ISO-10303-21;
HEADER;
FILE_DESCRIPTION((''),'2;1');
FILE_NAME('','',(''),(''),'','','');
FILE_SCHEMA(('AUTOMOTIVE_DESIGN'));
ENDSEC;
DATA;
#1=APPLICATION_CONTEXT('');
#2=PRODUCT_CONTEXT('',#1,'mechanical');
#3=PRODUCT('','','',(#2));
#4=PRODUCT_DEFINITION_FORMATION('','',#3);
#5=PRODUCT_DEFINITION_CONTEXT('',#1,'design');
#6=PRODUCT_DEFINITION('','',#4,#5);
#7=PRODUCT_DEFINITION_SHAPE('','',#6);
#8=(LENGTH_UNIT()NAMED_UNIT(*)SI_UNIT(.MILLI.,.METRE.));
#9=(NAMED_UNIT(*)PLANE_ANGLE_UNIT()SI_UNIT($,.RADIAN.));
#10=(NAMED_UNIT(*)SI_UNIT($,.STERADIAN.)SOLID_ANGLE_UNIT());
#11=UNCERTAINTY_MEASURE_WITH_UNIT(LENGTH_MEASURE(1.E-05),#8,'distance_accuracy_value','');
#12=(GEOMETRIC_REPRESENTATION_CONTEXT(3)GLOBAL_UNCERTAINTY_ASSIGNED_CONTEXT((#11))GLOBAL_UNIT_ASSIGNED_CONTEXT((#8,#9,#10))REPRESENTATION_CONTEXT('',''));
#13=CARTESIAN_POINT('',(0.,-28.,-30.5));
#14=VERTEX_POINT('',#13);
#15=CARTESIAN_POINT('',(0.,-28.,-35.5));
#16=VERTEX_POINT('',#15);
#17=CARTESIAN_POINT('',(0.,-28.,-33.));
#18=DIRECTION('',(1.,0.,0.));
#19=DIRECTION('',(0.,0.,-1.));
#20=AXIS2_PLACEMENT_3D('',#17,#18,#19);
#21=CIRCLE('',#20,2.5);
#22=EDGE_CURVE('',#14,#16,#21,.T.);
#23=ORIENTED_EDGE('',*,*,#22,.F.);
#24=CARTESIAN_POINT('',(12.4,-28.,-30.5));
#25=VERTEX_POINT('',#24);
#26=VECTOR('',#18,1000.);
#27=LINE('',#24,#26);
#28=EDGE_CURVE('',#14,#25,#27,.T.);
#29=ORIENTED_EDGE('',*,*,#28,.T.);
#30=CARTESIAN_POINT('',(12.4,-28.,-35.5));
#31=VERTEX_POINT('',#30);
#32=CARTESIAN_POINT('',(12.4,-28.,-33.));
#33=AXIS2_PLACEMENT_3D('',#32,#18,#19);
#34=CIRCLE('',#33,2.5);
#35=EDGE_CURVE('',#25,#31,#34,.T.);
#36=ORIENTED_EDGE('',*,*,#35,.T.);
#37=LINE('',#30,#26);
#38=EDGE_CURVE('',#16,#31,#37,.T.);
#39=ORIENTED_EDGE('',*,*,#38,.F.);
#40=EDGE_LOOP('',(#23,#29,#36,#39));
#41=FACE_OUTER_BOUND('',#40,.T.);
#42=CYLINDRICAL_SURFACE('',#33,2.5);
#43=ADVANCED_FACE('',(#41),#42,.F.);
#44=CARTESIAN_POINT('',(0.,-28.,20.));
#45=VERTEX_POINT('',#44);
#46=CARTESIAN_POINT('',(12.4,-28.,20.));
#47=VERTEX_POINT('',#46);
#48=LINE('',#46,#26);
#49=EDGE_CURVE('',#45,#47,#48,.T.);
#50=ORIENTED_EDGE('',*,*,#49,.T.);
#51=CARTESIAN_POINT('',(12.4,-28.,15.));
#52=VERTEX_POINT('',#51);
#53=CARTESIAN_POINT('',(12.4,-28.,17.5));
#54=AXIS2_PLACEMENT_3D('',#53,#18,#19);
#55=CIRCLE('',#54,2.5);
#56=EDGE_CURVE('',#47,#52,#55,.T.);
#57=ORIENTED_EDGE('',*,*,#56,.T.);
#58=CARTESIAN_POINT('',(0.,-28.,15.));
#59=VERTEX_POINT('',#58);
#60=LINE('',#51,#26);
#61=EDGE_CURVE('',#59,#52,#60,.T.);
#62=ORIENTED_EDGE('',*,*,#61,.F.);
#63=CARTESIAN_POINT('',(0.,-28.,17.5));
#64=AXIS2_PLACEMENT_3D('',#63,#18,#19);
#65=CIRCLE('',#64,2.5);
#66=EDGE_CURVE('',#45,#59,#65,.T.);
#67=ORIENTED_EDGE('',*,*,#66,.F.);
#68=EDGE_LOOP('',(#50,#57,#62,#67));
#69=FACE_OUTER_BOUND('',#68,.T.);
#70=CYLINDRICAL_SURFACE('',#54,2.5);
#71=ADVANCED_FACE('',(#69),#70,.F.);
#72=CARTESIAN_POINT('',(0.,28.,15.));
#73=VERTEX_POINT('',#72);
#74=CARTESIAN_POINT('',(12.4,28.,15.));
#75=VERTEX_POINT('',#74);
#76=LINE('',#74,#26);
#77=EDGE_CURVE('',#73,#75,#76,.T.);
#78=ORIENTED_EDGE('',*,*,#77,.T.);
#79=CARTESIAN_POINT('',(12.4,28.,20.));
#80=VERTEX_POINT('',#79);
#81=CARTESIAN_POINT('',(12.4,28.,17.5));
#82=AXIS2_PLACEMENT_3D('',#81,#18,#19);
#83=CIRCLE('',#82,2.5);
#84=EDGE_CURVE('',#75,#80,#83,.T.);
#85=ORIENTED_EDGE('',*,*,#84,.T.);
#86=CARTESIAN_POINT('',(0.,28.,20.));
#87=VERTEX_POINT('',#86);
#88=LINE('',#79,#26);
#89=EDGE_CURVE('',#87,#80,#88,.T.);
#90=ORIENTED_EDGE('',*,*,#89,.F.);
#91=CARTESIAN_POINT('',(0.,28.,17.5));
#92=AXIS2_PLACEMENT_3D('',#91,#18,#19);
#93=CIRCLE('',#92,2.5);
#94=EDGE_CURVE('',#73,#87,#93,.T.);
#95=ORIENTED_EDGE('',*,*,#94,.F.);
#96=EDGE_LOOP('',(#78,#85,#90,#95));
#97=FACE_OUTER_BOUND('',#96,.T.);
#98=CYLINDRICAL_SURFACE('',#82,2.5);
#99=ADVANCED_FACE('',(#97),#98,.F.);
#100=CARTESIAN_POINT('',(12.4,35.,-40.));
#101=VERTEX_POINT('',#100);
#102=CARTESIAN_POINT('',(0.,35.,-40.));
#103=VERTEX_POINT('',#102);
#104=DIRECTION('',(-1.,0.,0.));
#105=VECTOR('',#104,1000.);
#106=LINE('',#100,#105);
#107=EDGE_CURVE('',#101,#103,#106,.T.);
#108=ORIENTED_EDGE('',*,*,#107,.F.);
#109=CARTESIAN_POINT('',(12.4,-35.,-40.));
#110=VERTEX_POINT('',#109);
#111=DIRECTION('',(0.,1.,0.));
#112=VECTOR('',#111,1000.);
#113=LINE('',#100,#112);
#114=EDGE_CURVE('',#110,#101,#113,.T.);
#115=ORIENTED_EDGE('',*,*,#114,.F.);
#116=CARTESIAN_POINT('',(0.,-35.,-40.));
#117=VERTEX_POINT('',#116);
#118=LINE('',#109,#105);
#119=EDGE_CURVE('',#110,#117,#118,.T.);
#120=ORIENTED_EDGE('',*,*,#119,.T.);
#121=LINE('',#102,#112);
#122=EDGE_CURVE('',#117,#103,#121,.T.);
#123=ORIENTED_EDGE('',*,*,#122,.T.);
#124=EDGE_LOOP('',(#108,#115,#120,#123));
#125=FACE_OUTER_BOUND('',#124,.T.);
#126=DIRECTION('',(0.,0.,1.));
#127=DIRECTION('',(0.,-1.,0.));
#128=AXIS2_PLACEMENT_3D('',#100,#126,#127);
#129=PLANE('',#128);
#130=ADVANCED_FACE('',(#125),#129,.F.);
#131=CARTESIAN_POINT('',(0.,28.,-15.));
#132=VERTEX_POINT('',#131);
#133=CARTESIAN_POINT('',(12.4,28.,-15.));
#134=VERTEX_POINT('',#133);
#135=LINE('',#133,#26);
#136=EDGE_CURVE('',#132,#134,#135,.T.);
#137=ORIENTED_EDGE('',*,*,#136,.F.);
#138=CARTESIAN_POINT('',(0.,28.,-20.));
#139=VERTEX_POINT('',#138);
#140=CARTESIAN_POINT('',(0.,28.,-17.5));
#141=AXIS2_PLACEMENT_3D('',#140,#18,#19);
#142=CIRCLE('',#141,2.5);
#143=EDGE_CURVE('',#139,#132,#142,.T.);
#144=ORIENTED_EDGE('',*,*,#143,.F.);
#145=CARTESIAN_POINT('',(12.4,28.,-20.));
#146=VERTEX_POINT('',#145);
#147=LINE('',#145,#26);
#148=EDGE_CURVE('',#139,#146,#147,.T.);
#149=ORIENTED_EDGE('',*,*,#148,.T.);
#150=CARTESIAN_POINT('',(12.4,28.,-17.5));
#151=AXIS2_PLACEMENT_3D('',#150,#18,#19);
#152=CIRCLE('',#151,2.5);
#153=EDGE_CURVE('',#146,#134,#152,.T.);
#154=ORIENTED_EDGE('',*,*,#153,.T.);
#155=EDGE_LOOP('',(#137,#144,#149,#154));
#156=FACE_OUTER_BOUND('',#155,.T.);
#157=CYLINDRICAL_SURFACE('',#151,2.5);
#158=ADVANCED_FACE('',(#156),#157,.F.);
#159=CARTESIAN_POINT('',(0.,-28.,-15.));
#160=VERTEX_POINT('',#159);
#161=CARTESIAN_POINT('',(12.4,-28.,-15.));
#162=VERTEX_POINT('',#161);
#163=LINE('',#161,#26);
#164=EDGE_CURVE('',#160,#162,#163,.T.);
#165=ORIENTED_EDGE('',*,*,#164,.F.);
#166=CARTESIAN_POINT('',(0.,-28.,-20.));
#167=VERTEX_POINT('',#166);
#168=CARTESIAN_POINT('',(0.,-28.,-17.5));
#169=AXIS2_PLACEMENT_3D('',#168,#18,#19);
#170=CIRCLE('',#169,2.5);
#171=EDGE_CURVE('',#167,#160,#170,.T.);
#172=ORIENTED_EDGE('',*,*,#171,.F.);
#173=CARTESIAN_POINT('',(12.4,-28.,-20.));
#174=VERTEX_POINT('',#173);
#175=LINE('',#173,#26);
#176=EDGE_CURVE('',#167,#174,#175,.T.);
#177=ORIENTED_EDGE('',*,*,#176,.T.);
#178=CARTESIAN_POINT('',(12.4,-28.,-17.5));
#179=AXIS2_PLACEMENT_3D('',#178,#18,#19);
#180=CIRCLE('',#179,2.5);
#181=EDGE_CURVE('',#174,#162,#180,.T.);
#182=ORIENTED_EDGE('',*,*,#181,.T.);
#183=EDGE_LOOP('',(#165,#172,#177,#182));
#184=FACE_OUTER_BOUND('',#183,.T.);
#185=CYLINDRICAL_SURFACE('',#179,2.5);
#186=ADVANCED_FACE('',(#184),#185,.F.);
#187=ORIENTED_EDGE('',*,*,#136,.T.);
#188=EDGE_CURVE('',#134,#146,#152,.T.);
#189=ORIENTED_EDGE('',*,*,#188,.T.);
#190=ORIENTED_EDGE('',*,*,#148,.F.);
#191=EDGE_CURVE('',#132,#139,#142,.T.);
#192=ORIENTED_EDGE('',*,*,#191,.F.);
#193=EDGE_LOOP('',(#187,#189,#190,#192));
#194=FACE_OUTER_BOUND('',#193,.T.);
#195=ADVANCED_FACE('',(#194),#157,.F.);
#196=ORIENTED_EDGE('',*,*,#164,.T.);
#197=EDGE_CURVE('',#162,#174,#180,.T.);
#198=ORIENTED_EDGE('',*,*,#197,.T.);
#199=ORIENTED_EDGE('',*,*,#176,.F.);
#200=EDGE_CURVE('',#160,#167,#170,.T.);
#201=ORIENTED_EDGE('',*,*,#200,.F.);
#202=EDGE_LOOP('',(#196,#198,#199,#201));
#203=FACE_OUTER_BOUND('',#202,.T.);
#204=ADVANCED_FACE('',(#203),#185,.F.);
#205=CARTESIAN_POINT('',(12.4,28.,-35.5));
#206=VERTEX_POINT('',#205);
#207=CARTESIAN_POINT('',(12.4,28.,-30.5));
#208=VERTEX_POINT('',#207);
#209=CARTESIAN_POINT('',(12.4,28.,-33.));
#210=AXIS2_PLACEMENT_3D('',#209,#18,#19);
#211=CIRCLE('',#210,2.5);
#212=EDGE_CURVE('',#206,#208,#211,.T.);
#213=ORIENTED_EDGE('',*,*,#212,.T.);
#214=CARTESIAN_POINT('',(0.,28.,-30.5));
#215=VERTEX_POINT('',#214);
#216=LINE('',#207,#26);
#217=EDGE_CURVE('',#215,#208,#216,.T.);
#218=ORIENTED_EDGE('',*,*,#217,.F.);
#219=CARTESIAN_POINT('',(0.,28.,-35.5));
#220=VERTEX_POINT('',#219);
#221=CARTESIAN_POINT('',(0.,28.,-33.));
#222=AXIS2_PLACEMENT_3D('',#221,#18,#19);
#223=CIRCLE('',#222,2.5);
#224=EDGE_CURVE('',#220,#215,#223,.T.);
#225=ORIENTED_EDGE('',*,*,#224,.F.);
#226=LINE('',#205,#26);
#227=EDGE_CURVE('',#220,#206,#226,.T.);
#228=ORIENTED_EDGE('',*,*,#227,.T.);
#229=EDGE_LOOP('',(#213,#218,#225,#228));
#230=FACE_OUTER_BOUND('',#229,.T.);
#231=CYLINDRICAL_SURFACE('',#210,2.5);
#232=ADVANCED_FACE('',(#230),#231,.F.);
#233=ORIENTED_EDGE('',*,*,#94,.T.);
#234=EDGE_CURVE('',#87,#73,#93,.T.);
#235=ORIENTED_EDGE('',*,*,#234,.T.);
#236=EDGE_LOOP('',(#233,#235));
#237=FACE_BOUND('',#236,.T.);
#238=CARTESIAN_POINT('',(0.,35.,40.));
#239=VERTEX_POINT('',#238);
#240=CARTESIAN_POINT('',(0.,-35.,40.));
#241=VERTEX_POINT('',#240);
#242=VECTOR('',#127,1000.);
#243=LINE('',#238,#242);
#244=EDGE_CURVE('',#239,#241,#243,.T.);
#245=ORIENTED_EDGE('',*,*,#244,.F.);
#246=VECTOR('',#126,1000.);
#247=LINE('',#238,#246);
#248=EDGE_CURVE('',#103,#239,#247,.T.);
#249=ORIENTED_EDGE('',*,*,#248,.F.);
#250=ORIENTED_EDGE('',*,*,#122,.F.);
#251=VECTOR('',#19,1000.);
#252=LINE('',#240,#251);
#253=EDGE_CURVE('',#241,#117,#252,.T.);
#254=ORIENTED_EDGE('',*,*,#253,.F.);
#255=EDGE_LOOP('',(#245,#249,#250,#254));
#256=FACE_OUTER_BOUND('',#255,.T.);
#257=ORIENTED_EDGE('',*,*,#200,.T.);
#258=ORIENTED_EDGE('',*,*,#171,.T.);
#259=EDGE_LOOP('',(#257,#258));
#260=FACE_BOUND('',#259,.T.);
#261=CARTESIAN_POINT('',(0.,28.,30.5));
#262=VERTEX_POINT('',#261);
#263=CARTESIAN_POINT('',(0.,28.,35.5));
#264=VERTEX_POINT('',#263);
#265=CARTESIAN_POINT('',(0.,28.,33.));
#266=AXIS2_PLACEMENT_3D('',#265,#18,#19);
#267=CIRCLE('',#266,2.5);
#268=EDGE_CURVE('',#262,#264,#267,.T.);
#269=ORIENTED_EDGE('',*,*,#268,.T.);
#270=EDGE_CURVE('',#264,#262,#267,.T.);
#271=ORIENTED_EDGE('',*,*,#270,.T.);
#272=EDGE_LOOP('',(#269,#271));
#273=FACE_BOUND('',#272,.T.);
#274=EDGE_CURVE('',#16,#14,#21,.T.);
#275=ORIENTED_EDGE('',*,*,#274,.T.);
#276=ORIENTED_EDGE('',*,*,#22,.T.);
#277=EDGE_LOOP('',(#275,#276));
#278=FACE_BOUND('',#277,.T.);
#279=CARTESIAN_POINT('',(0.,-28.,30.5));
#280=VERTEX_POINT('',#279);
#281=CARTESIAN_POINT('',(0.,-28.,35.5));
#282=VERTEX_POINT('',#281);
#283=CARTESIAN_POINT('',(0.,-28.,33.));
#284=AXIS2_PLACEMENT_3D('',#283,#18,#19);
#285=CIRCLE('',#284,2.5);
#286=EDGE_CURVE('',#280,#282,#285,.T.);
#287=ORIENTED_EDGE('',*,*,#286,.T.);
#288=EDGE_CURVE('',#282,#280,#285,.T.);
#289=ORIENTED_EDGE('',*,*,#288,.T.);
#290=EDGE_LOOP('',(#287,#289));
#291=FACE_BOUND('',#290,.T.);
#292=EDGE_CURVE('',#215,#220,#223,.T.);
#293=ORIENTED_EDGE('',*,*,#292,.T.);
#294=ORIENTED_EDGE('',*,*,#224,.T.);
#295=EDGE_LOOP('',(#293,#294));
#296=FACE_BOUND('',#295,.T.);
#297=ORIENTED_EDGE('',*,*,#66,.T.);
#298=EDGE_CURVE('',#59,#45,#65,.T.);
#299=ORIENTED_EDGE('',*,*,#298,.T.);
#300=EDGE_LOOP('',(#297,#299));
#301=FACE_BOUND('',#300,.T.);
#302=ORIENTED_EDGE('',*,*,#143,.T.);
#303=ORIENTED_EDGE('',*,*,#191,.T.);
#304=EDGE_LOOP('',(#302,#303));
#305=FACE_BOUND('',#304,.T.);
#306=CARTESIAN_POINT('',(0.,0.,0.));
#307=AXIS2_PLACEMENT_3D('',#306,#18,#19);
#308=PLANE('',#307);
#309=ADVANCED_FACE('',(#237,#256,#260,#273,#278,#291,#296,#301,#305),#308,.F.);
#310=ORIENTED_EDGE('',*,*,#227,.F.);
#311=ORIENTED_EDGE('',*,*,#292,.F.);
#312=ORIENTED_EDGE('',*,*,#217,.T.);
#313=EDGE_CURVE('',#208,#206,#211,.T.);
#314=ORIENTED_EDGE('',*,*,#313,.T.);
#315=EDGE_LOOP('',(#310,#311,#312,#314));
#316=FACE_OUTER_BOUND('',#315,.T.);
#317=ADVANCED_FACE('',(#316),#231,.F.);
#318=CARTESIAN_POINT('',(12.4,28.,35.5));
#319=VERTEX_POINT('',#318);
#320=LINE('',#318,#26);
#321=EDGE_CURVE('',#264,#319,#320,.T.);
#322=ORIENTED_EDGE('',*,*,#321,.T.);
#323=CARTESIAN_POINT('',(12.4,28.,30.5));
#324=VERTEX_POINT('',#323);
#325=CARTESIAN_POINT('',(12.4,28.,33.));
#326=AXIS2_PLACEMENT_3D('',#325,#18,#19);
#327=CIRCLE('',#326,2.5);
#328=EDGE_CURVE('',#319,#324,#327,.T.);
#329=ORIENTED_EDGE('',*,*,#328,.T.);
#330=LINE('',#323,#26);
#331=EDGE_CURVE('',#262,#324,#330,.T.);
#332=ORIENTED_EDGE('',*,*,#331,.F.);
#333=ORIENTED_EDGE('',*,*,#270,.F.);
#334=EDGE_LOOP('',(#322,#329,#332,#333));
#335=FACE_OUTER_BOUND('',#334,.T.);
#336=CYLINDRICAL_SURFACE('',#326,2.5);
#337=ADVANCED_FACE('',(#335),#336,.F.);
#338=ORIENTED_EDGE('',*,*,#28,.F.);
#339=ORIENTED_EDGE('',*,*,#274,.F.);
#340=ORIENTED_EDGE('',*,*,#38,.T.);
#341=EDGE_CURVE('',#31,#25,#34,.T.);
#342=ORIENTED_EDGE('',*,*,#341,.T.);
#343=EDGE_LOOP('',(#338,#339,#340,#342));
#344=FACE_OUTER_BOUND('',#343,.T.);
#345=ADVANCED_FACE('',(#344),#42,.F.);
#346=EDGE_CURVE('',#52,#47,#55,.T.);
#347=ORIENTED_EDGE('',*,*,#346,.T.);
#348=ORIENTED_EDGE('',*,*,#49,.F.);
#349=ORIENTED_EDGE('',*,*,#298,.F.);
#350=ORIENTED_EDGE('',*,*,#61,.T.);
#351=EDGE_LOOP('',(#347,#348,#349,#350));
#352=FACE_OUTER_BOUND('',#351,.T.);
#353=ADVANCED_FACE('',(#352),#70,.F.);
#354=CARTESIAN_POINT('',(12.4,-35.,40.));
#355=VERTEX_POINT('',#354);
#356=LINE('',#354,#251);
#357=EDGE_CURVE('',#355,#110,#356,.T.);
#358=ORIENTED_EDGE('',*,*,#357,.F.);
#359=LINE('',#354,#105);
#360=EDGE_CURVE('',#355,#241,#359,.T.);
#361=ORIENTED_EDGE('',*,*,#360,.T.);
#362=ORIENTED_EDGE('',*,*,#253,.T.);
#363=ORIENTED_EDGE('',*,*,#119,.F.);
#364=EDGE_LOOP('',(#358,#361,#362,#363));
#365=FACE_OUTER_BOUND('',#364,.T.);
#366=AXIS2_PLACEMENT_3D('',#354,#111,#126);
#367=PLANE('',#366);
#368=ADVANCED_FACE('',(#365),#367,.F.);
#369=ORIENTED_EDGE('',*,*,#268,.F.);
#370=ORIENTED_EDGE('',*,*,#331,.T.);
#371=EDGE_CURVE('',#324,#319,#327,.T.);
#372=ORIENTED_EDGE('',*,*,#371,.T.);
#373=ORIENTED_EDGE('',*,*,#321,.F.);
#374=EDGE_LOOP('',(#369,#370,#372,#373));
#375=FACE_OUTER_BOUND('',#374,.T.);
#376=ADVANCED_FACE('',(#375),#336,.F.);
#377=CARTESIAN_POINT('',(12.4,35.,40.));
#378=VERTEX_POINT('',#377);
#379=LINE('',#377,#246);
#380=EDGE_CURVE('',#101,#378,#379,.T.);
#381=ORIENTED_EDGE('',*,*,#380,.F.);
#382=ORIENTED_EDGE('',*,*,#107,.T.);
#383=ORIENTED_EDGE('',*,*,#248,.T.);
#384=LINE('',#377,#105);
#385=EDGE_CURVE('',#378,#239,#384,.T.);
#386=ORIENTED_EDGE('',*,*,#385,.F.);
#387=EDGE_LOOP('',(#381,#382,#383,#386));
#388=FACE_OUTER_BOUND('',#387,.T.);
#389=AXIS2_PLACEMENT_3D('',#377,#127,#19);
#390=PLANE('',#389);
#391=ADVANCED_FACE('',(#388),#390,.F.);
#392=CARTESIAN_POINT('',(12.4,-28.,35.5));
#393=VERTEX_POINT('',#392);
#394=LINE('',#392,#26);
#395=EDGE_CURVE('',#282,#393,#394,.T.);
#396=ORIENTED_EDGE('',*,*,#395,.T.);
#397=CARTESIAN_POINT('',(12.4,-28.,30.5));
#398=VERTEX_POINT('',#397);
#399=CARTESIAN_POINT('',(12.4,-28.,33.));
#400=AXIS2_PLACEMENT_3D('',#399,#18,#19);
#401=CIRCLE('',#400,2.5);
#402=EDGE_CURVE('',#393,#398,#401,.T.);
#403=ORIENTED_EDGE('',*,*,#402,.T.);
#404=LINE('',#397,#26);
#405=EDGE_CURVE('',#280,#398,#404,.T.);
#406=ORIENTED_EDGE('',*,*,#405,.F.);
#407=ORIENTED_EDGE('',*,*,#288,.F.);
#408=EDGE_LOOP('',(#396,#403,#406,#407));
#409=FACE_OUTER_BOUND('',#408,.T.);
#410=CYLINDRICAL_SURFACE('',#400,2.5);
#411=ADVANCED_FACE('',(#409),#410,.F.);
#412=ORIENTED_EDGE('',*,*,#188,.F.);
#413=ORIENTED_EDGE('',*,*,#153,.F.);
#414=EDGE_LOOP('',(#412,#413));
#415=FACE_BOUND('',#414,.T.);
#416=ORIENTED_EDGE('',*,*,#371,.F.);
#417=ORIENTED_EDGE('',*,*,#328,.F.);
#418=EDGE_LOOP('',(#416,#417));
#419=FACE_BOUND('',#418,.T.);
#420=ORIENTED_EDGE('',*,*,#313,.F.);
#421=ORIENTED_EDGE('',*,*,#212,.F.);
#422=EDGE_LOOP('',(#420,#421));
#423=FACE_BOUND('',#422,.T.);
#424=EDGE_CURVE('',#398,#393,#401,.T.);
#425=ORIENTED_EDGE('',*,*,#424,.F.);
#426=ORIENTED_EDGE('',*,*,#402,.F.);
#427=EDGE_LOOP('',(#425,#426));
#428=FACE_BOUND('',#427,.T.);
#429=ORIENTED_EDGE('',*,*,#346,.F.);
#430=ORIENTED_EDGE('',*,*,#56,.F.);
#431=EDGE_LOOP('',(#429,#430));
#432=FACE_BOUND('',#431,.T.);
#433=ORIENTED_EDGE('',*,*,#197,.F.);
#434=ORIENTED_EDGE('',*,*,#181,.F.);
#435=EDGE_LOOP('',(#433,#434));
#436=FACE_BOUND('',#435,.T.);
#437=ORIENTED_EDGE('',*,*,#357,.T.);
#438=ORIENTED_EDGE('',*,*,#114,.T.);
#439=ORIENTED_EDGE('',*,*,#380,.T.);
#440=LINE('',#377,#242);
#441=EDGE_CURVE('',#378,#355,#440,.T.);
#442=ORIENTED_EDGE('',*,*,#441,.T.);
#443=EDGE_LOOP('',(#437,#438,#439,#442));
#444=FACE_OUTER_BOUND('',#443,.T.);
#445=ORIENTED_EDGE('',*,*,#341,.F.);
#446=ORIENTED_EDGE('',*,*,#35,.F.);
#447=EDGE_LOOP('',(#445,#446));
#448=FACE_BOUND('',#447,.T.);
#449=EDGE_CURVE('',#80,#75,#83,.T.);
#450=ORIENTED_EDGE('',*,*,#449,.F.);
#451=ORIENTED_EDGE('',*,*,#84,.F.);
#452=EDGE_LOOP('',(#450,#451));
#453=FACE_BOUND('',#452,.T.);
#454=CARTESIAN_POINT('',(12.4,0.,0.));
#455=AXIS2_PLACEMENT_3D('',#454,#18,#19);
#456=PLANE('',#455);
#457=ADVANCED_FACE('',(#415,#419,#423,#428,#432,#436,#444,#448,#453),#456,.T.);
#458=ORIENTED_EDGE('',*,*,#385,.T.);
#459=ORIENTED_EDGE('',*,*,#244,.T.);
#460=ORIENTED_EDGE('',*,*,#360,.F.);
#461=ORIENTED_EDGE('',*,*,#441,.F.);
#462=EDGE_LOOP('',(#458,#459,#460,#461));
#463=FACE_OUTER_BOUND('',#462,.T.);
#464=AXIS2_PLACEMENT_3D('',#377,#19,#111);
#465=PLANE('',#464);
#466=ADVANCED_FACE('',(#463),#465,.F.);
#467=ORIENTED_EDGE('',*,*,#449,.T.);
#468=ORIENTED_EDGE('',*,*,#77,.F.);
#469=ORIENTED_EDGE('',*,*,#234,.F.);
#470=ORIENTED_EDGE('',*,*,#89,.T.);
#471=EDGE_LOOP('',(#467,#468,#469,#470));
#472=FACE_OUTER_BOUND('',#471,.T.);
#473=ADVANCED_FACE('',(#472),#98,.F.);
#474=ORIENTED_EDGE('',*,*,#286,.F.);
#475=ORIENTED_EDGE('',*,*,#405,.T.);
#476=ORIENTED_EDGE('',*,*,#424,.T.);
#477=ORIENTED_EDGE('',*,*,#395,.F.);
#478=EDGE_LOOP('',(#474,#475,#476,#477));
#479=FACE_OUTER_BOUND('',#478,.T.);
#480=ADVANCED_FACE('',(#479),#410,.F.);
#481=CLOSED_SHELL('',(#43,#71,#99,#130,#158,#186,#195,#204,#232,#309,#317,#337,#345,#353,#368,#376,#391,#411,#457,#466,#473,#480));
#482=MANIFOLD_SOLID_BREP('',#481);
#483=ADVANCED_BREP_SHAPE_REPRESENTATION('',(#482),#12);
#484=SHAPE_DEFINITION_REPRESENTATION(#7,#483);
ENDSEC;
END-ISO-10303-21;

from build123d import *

# Parameters (mm, degrees)
SKETCH_1_W             = 80
SKETCH_1_H             = 70
EXTRUDE_1_DEPTH        = 12.4
HOLE_WIZARD_M6_1_D     = 5
HOLE_WIZARD_M6_1_DEPTH = 15
HOLE_WIZARD_M6_1_TIP   = 1.502151548
HOLE_WIZARD_M6_2_D     = 5


with BuildPart() as part:
    # 草图1 → 凸台-拉伸1 (new body)
    with BuildSketch(Plane(origin=(0, 0, 0), x_dir=(0, 0, -1), z_dir=(1, 0, 0))):
        Rectangle(SKETCH_1_W, SKETCH_1_H)
    extrude(amount=EXTRUDE_1_DEPTH)

    # M6 螺纹孔1
    with Locations(Plane(origin=(12.4, 0, 0), x_dir=(0, 0, -1), z_dir=(1, 0, 0))):
        with Locations((-17.5, 28), (17.5, 28), (-17.5, -28), (17.5, -28)):
            Hole(HOLE_WIZARD_M6_1_D / 2, depth=HOLE_WIZARD_M6_1_DEPTH)
            with Locations((0, 0, -(HOLE_WIZARD_M6_1_DEPTH + HOLE_WIZARD_M6_1_TIP / 2))):  # 118° drill point
                Cone(0, HOLE_WIZARD_M6_1_D / 2, HOLE_WIZARD_M6_1_TIP, mode=Mode.SUBTRACT)

    # M6 螺纹孔2 (through all)
    with Locations(Plane(origin=(12.4, 0, 0), x_dir=(0, 0, -1), z_dir=(1, 0, 0))):
        with Locations((-33, 28), (-33, -28), (33, -28), (33, 28)):
            Hole(HOLE_WIZARD_M6_2_D / 2)


solid = part.part
